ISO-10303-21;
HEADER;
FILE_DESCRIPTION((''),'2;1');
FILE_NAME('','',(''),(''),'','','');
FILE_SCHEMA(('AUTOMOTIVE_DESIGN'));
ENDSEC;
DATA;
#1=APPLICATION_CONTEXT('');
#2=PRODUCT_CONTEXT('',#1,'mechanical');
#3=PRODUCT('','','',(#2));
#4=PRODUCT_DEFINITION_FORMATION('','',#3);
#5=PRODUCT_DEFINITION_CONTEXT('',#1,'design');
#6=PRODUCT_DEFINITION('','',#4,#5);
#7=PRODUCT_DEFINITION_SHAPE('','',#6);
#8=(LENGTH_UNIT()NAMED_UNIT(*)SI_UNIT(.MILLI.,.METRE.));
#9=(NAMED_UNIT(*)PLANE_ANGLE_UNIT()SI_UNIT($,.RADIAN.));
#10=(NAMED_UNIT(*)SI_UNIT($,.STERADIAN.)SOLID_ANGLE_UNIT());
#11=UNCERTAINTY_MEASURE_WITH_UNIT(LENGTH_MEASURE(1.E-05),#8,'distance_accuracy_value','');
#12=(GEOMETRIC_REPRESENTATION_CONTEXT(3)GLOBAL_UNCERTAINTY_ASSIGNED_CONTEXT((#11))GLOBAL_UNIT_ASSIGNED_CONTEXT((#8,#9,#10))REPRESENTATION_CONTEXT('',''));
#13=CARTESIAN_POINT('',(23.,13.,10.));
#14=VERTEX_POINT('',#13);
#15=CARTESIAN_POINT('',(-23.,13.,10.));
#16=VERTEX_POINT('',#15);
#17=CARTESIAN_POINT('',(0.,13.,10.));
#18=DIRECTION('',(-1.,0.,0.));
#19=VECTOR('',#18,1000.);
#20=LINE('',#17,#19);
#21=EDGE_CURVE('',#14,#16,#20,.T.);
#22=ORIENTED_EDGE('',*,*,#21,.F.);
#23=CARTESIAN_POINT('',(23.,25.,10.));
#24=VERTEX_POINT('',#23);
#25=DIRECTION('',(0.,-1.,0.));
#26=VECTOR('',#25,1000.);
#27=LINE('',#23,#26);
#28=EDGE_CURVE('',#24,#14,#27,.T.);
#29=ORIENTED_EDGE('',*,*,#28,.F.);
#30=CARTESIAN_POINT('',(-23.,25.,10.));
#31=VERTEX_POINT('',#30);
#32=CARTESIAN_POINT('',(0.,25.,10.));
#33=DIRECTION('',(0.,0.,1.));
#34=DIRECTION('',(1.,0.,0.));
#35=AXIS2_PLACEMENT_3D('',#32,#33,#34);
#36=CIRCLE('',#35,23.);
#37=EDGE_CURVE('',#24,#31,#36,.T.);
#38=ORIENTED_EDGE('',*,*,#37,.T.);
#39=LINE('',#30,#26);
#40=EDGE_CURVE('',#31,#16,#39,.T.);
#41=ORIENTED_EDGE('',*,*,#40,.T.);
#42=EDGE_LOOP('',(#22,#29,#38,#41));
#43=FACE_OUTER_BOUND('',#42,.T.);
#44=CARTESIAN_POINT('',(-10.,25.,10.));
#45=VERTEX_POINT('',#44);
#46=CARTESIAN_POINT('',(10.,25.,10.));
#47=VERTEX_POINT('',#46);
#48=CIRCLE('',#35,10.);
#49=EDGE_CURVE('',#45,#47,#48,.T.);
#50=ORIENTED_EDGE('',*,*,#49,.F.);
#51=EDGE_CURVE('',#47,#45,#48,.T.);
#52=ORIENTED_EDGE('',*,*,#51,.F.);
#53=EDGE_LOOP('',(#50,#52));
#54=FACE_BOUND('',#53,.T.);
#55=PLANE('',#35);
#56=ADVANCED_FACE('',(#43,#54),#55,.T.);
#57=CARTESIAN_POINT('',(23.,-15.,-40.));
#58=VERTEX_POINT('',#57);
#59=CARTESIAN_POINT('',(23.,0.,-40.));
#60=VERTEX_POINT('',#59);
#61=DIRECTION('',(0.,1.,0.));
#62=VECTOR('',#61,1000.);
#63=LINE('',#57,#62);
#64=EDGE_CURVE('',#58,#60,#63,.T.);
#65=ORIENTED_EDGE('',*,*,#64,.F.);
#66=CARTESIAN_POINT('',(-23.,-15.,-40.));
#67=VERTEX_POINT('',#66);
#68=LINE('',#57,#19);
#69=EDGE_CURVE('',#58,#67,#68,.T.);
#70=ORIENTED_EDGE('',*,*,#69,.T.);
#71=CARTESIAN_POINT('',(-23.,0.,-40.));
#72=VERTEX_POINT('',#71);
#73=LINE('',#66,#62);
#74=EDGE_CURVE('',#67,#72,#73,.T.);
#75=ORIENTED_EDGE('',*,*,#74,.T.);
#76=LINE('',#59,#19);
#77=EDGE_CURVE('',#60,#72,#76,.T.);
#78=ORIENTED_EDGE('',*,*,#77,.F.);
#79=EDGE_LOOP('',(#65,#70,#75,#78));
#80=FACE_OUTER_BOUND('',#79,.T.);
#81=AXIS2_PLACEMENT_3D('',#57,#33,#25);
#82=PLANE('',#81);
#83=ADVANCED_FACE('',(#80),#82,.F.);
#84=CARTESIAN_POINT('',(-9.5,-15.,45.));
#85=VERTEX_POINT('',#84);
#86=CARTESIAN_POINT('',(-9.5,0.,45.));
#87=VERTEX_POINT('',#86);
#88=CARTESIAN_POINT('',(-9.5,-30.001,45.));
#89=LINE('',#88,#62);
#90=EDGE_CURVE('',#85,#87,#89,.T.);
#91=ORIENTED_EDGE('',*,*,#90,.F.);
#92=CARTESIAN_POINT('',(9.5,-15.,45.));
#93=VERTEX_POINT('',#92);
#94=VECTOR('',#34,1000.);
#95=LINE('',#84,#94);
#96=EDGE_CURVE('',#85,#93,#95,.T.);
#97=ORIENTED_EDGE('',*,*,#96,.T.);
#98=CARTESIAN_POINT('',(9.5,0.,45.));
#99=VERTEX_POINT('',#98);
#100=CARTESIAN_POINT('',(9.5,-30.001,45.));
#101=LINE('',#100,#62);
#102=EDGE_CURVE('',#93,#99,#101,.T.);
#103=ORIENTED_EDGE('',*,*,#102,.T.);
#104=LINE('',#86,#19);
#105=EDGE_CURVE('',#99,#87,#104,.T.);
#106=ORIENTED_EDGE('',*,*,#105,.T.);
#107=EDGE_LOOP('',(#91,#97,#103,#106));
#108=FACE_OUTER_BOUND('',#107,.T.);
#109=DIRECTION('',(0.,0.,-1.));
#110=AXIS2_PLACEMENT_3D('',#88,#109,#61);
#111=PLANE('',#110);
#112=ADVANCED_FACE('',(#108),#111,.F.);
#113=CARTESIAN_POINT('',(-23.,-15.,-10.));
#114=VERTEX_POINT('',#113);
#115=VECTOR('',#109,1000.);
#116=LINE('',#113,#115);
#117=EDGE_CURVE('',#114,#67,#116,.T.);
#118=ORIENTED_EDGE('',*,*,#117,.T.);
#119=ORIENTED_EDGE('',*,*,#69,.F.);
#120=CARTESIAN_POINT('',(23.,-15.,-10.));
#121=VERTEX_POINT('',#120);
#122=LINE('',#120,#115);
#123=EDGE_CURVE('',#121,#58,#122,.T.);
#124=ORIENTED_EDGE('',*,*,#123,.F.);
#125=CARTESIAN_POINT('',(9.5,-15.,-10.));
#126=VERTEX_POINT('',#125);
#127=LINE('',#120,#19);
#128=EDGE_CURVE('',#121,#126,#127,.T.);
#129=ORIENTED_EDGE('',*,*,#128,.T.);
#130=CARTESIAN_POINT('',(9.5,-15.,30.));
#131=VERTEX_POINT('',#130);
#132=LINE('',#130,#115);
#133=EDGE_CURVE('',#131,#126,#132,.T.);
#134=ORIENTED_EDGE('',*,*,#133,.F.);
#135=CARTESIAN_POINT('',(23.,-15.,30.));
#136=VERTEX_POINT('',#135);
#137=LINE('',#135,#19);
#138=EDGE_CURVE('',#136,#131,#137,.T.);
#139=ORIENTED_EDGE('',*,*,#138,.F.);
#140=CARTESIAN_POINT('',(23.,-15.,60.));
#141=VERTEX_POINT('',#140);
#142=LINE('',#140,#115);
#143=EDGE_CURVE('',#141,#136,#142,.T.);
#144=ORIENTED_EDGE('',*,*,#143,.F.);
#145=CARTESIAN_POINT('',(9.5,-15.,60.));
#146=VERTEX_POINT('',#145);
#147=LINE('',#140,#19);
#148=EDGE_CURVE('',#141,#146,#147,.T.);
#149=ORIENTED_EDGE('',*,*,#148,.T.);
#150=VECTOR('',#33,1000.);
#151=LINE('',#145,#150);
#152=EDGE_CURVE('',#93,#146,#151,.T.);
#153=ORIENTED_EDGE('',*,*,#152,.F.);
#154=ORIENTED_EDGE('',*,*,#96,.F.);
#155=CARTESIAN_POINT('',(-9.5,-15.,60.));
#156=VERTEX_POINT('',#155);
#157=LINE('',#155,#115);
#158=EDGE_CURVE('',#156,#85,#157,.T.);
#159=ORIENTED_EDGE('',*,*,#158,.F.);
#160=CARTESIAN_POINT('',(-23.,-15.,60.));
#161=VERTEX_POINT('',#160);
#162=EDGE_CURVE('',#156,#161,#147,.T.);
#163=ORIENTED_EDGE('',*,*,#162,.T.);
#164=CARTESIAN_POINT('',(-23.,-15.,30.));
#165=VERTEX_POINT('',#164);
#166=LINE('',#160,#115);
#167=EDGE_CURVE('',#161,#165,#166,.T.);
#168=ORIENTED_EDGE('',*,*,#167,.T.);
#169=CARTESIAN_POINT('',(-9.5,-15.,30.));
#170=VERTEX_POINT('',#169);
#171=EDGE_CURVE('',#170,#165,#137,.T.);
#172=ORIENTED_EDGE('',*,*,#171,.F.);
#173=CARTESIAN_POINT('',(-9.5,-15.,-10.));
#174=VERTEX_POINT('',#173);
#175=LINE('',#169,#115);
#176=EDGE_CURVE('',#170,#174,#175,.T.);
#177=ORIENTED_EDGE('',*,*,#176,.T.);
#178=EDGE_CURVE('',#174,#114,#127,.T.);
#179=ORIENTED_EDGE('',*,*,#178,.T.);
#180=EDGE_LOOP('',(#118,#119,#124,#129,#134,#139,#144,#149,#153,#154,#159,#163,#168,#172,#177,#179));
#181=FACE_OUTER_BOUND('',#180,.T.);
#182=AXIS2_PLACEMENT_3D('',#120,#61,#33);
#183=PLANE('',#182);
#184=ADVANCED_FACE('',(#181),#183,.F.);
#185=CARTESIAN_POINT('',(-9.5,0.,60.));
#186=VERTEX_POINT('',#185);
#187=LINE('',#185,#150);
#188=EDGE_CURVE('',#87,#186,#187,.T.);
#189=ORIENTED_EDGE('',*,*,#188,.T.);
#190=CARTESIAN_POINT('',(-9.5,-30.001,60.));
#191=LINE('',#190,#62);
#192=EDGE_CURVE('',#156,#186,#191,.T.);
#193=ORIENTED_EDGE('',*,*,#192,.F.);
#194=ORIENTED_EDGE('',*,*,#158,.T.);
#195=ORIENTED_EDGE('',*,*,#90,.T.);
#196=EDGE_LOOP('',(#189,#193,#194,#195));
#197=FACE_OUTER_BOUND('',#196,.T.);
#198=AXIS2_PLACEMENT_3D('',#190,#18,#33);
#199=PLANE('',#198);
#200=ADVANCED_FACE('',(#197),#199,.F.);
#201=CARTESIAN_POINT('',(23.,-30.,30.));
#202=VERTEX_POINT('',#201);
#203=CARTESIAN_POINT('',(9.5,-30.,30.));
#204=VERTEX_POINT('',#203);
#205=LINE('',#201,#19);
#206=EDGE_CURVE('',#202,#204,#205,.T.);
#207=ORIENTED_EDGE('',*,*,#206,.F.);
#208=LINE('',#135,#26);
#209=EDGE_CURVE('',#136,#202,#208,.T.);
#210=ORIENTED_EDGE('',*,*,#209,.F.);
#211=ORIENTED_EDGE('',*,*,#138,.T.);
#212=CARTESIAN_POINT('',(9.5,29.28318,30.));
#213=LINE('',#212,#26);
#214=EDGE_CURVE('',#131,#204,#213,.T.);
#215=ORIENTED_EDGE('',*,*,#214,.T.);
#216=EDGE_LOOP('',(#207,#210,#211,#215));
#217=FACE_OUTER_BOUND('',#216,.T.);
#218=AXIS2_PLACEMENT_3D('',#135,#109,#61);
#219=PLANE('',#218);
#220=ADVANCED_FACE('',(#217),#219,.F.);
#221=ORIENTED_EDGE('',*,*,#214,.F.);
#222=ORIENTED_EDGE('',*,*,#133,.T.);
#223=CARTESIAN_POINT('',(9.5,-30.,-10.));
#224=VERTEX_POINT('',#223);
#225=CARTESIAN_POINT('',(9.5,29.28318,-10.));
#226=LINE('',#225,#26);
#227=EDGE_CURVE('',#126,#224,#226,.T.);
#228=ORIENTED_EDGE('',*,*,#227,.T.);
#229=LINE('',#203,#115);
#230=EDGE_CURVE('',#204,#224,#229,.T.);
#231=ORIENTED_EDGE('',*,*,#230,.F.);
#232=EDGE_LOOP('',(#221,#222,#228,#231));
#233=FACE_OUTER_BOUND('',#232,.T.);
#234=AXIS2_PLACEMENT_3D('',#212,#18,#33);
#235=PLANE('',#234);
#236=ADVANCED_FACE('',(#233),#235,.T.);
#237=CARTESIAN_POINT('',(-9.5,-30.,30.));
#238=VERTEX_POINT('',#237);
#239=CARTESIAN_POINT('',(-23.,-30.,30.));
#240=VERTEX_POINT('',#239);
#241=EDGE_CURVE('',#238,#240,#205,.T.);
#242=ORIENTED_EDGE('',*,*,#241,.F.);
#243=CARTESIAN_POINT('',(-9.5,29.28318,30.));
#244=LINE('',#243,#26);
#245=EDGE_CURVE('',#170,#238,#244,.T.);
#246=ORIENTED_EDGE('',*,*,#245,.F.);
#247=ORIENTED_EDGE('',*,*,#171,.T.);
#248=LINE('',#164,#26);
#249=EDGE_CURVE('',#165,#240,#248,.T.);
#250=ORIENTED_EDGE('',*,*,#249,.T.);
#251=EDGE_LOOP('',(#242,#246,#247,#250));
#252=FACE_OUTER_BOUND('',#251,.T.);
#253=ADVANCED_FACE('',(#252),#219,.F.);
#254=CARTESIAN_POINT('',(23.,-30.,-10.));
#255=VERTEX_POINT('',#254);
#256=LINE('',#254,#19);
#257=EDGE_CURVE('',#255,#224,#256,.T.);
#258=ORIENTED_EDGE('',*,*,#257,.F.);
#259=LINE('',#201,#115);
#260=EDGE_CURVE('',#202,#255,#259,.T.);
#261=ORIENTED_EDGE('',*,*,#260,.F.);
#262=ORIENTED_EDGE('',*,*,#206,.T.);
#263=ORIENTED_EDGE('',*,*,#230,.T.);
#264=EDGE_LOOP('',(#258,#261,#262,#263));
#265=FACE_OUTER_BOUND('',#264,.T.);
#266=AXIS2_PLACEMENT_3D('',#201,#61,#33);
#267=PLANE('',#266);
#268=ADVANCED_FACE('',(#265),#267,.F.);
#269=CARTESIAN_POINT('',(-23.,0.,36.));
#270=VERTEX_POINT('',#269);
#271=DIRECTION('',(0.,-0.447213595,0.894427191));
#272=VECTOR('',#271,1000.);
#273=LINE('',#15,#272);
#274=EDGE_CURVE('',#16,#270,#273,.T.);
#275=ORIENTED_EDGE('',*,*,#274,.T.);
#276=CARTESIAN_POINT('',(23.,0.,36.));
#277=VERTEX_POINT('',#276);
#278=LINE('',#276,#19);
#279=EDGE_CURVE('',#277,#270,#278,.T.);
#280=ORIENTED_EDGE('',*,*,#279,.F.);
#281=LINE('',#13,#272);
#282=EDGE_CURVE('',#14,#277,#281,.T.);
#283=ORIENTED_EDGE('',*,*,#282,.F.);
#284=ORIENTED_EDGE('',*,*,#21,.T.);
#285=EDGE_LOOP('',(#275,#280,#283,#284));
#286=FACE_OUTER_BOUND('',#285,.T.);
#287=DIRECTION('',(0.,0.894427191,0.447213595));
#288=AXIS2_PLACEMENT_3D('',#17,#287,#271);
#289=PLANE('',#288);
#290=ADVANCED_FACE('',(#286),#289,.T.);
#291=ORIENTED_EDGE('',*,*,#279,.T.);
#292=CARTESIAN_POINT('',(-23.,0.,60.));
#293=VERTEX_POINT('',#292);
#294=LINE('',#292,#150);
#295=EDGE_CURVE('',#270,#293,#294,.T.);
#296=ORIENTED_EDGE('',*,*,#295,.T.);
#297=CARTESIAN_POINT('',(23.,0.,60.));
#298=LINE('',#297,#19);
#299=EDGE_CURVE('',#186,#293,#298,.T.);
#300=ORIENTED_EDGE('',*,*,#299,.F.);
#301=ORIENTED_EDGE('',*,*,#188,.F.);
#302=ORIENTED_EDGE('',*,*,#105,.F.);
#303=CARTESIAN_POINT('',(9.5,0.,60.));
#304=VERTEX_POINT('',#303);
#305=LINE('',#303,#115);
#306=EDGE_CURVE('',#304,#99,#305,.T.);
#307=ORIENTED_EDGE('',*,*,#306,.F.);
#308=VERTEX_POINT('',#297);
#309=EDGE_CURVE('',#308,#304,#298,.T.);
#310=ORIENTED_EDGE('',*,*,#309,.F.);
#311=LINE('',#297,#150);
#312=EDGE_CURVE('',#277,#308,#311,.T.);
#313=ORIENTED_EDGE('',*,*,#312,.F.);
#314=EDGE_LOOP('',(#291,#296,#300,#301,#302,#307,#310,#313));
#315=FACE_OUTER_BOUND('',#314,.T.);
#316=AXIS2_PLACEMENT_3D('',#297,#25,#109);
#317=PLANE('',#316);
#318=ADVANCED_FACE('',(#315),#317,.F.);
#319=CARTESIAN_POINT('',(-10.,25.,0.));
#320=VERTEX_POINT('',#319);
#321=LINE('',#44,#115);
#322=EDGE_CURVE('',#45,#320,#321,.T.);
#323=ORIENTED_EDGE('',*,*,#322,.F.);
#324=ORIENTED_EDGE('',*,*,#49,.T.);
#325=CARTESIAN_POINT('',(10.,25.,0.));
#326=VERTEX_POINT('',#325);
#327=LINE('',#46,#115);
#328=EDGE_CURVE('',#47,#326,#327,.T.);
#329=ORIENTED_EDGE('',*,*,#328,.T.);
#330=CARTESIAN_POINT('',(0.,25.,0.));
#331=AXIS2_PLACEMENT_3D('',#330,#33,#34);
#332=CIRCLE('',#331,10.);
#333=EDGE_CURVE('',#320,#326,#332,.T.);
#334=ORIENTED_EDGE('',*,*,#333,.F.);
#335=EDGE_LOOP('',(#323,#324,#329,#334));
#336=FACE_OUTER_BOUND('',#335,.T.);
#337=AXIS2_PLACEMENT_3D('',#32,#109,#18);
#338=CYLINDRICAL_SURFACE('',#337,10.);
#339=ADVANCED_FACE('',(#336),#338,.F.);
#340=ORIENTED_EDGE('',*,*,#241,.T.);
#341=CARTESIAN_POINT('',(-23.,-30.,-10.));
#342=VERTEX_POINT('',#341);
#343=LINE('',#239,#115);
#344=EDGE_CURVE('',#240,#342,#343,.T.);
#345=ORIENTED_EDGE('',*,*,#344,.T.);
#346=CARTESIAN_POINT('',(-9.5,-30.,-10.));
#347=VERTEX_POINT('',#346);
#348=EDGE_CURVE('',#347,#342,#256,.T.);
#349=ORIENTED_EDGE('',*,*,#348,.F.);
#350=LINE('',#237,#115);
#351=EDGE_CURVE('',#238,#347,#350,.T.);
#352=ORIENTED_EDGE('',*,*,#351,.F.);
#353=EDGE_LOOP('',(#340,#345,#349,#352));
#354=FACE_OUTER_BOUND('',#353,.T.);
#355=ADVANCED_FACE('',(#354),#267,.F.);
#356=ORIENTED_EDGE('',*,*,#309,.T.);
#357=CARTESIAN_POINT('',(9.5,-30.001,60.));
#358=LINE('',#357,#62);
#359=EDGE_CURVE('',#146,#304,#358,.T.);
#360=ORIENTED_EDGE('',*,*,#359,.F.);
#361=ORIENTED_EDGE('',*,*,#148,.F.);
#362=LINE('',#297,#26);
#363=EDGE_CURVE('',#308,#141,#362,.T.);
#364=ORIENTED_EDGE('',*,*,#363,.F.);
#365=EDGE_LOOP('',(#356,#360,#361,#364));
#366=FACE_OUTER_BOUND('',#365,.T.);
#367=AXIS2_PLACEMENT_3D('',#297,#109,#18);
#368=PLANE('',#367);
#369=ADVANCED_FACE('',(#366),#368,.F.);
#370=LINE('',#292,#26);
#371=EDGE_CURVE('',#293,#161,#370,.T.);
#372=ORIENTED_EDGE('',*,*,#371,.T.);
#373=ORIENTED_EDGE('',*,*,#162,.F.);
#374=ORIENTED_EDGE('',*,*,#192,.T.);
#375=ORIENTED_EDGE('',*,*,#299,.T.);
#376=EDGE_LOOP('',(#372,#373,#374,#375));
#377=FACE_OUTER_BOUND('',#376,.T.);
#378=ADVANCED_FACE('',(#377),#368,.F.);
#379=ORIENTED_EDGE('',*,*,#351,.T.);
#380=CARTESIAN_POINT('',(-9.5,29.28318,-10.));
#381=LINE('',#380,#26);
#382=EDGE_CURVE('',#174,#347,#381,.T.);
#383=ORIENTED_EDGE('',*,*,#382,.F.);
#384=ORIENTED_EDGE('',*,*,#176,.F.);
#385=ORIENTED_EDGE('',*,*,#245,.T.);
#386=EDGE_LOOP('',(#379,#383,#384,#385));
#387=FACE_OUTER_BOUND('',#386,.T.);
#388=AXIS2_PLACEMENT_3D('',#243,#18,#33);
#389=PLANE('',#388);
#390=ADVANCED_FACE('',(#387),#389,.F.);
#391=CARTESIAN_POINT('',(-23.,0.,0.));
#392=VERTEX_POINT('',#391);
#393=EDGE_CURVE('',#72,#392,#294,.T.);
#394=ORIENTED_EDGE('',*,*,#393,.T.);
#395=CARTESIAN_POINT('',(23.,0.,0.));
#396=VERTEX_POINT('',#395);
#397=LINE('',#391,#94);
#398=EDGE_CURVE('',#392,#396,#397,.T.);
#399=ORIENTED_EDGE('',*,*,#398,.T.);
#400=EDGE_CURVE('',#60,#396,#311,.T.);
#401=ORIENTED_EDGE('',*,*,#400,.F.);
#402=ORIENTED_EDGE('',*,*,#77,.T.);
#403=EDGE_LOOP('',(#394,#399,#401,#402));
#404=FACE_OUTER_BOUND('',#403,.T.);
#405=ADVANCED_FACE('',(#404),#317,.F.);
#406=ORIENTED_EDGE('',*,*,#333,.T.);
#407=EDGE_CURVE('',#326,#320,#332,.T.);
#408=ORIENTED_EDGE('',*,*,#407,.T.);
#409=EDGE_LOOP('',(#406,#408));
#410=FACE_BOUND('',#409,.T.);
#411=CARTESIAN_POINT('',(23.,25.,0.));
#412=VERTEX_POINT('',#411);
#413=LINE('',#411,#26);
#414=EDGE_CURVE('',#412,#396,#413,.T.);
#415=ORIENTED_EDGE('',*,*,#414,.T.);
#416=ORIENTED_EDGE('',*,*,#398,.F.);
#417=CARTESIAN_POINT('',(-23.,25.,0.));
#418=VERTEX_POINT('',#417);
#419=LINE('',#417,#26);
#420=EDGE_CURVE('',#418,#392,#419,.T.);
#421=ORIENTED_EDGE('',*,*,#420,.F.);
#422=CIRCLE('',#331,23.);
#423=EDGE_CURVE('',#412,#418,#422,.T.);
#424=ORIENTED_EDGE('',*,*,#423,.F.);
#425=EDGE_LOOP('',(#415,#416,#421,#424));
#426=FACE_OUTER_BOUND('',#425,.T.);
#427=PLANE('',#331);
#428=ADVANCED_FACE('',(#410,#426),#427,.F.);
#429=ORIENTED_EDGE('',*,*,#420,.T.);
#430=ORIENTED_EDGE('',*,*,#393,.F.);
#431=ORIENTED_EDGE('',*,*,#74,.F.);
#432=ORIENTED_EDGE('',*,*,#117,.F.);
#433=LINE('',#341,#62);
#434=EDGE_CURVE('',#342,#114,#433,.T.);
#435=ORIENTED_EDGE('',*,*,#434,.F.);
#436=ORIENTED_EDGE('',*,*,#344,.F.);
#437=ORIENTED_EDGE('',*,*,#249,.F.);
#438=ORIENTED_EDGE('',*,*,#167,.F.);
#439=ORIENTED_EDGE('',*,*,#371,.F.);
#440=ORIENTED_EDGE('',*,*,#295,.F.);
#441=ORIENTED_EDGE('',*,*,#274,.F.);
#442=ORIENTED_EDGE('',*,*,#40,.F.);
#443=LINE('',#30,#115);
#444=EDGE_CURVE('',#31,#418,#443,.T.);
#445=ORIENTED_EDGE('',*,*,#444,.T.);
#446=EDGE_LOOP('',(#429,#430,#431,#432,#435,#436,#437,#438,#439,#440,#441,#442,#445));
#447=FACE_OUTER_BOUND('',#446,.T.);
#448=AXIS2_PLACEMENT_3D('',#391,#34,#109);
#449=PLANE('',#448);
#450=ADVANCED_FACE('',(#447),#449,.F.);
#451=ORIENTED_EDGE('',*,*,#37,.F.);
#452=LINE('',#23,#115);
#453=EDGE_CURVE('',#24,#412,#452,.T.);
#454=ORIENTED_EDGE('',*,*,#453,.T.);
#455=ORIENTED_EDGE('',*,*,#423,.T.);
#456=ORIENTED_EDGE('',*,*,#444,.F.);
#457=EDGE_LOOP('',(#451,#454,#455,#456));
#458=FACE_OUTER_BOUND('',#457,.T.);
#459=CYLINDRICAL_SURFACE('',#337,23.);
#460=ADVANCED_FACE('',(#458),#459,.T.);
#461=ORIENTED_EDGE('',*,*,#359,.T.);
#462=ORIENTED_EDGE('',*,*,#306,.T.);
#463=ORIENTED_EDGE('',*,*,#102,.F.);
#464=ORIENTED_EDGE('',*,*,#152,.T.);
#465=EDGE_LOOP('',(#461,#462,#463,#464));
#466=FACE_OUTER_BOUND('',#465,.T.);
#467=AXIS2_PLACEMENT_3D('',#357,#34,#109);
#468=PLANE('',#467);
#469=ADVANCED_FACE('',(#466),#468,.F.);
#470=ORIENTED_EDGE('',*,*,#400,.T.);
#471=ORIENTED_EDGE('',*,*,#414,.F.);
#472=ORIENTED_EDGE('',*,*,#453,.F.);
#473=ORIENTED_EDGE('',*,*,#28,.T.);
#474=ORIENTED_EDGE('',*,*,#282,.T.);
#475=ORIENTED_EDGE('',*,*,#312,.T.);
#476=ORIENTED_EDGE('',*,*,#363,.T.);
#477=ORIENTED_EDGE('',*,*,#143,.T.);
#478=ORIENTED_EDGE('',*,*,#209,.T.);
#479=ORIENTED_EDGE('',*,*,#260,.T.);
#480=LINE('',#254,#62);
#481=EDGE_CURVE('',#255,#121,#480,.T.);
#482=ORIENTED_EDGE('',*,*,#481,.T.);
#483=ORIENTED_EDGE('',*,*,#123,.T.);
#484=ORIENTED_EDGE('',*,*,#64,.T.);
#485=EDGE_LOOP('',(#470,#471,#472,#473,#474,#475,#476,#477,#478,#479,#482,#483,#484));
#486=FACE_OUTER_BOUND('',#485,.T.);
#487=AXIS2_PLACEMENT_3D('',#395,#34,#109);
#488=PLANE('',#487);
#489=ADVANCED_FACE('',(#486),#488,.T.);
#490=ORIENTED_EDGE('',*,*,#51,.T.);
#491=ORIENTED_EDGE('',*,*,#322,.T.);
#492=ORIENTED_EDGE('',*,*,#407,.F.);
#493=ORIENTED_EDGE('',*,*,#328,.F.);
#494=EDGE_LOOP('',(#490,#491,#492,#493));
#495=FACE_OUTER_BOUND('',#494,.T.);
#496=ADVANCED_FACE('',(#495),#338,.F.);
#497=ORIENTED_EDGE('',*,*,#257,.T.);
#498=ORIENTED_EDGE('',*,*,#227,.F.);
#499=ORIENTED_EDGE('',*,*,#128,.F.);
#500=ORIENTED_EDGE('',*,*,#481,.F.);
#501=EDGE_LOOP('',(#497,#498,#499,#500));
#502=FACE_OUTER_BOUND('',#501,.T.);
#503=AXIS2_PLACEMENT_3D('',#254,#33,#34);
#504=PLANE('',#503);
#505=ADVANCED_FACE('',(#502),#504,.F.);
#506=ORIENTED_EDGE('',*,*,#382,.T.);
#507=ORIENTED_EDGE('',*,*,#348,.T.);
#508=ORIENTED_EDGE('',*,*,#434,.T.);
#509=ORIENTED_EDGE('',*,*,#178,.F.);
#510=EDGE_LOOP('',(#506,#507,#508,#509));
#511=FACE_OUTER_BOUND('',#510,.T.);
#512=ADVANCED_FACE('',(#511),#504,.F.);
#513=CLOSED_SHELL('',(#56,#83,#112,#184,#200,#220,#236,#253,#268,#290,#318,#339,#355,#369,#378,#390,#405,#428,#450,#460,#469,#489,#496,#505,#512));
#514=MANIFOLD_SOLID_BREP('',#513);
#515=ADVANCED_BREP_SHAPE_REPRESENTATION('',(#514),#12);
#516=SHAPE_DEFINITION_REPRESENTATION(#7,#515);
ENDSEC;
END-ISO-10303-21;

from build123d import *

# Parameters (mm, degrees)
BASE_BODY_DEPTH           = 23
FORK_SLOT_19X15_REACH     = 72.915
FORK_SLOT_SKETCH_W        = 19
FORK_SLOT_SKETCH_H        = 15
CHANNEL_CUT_SKETCH_W      = 19
CHANNEL_CUT_SKETCH_H      = 40
THIN_CHANNEL_CUT_19_DEPTH = 15
LUG_SKETCH_R              = 10
LUG_WITH_BORE_DEPTH       = 10
SUPPORT_RIB_REACH         = 82.206
SUPPORT_RIB_SKETCH_WALL_W = 191.480853336
SUPPORT_RIB_SKETCH_WALL_H = 46


with BuildPart() as part:
    # Base Profile Sketch → Base Body (new, symmetric)
    with BuildSketch(Plane(origin=(0, 0, 0), x_dir=(0, 0, -1), z_dir=(1, 0, 0))):
        Polygon((-60, 0), (40, 0), (40, -15), (10, -15), (10, -30), (-30, -30), (-30, -15), (-60, -15), align=None)
    extrude(amount=BASE_BODY_DEPTH, both=True)

    # Fork Slot Sketch → Fork Slot 19x15 (cut, up to next)
    with BuildSketch(Plane(origin=(0, 0, 0), x_dir=(1, 0, 0), z_dir=(0, 1, 0)), mode=Mode.PRIVATE) as fork_slot_19x15_sk1:
        with Locations((0, -52.5)):
            Rectangle(FORK_SLOT_SKETCH_W, FORK_SLOT_SKETCH_H)
    fork_slot_19x15_tool1 = extrude(fork_slot_19x15_sk1.sketch, amount=-FORK_SLOT_19X15_REACH, mode=Mode.PRIVATE) & part.part
    add(fork_slot_19x15_tool1.solids().sort_by_distance((0, 0, 52.5))[0], mode=Mode.SUBTRACT)

    # Channel Cut Sketch → Thin Channel Cut 19 (cut)
    with BuildSketch(Plane.XZ.offset(30)):
        with Locations((0, 10)):
            Rectangle(CHANNEL_CUT_SKETCH_W, CHANNEL_CUT_SKETCH_H)
    extrude(amount=-THIN_CHANNEL_CUT_19_DEPTH, mode=Mode.SUBTRACT)

    # Lug Sketch → Lug with Bore (add)
    with BuildSketch(Plane.XY):
        with BuildLine():
            Line((23, 25), (23, 0))
            Line((23, 0), (-23, 0))
            Line((-23, 0), (-23, 25))
            ThreePointArc((-23, 25), (0, 48), (23, 25))
        make_face()
        with Locations((0, 25)):
            Circle(LUG_SKETCH_R, mode=Mode.SUBTRACT)
    extrude(amount=LUG_WITH_BORE_DEPTH)

    # Support Rib Sketch wall → Support Rib (add, up to next)
    with BuildSketch(Plane(origin=(0, 6.5, 23), x_dir=(0, -0.4472135955, 0.894427191), z_dir=(0, -0.894427191, -0.4472135955)), mode=Mode.PRIVATE) as support_rib_sk1:
        Rectangle(SUPPORT_RIB_SKETCH_WALL_W, SUPPORT_RIB_SKETCH_WALL_H)
    support_rib_tool1 = extrude(support_rib_sk1.sketch, amount=SUPPORT_RIB_REACH, mode=Mode.PRIVATE) - part.part
    add(support_rib_tool1.solids().sort_by_distance((0, 6.5, 23))[0])


solid = part.part
